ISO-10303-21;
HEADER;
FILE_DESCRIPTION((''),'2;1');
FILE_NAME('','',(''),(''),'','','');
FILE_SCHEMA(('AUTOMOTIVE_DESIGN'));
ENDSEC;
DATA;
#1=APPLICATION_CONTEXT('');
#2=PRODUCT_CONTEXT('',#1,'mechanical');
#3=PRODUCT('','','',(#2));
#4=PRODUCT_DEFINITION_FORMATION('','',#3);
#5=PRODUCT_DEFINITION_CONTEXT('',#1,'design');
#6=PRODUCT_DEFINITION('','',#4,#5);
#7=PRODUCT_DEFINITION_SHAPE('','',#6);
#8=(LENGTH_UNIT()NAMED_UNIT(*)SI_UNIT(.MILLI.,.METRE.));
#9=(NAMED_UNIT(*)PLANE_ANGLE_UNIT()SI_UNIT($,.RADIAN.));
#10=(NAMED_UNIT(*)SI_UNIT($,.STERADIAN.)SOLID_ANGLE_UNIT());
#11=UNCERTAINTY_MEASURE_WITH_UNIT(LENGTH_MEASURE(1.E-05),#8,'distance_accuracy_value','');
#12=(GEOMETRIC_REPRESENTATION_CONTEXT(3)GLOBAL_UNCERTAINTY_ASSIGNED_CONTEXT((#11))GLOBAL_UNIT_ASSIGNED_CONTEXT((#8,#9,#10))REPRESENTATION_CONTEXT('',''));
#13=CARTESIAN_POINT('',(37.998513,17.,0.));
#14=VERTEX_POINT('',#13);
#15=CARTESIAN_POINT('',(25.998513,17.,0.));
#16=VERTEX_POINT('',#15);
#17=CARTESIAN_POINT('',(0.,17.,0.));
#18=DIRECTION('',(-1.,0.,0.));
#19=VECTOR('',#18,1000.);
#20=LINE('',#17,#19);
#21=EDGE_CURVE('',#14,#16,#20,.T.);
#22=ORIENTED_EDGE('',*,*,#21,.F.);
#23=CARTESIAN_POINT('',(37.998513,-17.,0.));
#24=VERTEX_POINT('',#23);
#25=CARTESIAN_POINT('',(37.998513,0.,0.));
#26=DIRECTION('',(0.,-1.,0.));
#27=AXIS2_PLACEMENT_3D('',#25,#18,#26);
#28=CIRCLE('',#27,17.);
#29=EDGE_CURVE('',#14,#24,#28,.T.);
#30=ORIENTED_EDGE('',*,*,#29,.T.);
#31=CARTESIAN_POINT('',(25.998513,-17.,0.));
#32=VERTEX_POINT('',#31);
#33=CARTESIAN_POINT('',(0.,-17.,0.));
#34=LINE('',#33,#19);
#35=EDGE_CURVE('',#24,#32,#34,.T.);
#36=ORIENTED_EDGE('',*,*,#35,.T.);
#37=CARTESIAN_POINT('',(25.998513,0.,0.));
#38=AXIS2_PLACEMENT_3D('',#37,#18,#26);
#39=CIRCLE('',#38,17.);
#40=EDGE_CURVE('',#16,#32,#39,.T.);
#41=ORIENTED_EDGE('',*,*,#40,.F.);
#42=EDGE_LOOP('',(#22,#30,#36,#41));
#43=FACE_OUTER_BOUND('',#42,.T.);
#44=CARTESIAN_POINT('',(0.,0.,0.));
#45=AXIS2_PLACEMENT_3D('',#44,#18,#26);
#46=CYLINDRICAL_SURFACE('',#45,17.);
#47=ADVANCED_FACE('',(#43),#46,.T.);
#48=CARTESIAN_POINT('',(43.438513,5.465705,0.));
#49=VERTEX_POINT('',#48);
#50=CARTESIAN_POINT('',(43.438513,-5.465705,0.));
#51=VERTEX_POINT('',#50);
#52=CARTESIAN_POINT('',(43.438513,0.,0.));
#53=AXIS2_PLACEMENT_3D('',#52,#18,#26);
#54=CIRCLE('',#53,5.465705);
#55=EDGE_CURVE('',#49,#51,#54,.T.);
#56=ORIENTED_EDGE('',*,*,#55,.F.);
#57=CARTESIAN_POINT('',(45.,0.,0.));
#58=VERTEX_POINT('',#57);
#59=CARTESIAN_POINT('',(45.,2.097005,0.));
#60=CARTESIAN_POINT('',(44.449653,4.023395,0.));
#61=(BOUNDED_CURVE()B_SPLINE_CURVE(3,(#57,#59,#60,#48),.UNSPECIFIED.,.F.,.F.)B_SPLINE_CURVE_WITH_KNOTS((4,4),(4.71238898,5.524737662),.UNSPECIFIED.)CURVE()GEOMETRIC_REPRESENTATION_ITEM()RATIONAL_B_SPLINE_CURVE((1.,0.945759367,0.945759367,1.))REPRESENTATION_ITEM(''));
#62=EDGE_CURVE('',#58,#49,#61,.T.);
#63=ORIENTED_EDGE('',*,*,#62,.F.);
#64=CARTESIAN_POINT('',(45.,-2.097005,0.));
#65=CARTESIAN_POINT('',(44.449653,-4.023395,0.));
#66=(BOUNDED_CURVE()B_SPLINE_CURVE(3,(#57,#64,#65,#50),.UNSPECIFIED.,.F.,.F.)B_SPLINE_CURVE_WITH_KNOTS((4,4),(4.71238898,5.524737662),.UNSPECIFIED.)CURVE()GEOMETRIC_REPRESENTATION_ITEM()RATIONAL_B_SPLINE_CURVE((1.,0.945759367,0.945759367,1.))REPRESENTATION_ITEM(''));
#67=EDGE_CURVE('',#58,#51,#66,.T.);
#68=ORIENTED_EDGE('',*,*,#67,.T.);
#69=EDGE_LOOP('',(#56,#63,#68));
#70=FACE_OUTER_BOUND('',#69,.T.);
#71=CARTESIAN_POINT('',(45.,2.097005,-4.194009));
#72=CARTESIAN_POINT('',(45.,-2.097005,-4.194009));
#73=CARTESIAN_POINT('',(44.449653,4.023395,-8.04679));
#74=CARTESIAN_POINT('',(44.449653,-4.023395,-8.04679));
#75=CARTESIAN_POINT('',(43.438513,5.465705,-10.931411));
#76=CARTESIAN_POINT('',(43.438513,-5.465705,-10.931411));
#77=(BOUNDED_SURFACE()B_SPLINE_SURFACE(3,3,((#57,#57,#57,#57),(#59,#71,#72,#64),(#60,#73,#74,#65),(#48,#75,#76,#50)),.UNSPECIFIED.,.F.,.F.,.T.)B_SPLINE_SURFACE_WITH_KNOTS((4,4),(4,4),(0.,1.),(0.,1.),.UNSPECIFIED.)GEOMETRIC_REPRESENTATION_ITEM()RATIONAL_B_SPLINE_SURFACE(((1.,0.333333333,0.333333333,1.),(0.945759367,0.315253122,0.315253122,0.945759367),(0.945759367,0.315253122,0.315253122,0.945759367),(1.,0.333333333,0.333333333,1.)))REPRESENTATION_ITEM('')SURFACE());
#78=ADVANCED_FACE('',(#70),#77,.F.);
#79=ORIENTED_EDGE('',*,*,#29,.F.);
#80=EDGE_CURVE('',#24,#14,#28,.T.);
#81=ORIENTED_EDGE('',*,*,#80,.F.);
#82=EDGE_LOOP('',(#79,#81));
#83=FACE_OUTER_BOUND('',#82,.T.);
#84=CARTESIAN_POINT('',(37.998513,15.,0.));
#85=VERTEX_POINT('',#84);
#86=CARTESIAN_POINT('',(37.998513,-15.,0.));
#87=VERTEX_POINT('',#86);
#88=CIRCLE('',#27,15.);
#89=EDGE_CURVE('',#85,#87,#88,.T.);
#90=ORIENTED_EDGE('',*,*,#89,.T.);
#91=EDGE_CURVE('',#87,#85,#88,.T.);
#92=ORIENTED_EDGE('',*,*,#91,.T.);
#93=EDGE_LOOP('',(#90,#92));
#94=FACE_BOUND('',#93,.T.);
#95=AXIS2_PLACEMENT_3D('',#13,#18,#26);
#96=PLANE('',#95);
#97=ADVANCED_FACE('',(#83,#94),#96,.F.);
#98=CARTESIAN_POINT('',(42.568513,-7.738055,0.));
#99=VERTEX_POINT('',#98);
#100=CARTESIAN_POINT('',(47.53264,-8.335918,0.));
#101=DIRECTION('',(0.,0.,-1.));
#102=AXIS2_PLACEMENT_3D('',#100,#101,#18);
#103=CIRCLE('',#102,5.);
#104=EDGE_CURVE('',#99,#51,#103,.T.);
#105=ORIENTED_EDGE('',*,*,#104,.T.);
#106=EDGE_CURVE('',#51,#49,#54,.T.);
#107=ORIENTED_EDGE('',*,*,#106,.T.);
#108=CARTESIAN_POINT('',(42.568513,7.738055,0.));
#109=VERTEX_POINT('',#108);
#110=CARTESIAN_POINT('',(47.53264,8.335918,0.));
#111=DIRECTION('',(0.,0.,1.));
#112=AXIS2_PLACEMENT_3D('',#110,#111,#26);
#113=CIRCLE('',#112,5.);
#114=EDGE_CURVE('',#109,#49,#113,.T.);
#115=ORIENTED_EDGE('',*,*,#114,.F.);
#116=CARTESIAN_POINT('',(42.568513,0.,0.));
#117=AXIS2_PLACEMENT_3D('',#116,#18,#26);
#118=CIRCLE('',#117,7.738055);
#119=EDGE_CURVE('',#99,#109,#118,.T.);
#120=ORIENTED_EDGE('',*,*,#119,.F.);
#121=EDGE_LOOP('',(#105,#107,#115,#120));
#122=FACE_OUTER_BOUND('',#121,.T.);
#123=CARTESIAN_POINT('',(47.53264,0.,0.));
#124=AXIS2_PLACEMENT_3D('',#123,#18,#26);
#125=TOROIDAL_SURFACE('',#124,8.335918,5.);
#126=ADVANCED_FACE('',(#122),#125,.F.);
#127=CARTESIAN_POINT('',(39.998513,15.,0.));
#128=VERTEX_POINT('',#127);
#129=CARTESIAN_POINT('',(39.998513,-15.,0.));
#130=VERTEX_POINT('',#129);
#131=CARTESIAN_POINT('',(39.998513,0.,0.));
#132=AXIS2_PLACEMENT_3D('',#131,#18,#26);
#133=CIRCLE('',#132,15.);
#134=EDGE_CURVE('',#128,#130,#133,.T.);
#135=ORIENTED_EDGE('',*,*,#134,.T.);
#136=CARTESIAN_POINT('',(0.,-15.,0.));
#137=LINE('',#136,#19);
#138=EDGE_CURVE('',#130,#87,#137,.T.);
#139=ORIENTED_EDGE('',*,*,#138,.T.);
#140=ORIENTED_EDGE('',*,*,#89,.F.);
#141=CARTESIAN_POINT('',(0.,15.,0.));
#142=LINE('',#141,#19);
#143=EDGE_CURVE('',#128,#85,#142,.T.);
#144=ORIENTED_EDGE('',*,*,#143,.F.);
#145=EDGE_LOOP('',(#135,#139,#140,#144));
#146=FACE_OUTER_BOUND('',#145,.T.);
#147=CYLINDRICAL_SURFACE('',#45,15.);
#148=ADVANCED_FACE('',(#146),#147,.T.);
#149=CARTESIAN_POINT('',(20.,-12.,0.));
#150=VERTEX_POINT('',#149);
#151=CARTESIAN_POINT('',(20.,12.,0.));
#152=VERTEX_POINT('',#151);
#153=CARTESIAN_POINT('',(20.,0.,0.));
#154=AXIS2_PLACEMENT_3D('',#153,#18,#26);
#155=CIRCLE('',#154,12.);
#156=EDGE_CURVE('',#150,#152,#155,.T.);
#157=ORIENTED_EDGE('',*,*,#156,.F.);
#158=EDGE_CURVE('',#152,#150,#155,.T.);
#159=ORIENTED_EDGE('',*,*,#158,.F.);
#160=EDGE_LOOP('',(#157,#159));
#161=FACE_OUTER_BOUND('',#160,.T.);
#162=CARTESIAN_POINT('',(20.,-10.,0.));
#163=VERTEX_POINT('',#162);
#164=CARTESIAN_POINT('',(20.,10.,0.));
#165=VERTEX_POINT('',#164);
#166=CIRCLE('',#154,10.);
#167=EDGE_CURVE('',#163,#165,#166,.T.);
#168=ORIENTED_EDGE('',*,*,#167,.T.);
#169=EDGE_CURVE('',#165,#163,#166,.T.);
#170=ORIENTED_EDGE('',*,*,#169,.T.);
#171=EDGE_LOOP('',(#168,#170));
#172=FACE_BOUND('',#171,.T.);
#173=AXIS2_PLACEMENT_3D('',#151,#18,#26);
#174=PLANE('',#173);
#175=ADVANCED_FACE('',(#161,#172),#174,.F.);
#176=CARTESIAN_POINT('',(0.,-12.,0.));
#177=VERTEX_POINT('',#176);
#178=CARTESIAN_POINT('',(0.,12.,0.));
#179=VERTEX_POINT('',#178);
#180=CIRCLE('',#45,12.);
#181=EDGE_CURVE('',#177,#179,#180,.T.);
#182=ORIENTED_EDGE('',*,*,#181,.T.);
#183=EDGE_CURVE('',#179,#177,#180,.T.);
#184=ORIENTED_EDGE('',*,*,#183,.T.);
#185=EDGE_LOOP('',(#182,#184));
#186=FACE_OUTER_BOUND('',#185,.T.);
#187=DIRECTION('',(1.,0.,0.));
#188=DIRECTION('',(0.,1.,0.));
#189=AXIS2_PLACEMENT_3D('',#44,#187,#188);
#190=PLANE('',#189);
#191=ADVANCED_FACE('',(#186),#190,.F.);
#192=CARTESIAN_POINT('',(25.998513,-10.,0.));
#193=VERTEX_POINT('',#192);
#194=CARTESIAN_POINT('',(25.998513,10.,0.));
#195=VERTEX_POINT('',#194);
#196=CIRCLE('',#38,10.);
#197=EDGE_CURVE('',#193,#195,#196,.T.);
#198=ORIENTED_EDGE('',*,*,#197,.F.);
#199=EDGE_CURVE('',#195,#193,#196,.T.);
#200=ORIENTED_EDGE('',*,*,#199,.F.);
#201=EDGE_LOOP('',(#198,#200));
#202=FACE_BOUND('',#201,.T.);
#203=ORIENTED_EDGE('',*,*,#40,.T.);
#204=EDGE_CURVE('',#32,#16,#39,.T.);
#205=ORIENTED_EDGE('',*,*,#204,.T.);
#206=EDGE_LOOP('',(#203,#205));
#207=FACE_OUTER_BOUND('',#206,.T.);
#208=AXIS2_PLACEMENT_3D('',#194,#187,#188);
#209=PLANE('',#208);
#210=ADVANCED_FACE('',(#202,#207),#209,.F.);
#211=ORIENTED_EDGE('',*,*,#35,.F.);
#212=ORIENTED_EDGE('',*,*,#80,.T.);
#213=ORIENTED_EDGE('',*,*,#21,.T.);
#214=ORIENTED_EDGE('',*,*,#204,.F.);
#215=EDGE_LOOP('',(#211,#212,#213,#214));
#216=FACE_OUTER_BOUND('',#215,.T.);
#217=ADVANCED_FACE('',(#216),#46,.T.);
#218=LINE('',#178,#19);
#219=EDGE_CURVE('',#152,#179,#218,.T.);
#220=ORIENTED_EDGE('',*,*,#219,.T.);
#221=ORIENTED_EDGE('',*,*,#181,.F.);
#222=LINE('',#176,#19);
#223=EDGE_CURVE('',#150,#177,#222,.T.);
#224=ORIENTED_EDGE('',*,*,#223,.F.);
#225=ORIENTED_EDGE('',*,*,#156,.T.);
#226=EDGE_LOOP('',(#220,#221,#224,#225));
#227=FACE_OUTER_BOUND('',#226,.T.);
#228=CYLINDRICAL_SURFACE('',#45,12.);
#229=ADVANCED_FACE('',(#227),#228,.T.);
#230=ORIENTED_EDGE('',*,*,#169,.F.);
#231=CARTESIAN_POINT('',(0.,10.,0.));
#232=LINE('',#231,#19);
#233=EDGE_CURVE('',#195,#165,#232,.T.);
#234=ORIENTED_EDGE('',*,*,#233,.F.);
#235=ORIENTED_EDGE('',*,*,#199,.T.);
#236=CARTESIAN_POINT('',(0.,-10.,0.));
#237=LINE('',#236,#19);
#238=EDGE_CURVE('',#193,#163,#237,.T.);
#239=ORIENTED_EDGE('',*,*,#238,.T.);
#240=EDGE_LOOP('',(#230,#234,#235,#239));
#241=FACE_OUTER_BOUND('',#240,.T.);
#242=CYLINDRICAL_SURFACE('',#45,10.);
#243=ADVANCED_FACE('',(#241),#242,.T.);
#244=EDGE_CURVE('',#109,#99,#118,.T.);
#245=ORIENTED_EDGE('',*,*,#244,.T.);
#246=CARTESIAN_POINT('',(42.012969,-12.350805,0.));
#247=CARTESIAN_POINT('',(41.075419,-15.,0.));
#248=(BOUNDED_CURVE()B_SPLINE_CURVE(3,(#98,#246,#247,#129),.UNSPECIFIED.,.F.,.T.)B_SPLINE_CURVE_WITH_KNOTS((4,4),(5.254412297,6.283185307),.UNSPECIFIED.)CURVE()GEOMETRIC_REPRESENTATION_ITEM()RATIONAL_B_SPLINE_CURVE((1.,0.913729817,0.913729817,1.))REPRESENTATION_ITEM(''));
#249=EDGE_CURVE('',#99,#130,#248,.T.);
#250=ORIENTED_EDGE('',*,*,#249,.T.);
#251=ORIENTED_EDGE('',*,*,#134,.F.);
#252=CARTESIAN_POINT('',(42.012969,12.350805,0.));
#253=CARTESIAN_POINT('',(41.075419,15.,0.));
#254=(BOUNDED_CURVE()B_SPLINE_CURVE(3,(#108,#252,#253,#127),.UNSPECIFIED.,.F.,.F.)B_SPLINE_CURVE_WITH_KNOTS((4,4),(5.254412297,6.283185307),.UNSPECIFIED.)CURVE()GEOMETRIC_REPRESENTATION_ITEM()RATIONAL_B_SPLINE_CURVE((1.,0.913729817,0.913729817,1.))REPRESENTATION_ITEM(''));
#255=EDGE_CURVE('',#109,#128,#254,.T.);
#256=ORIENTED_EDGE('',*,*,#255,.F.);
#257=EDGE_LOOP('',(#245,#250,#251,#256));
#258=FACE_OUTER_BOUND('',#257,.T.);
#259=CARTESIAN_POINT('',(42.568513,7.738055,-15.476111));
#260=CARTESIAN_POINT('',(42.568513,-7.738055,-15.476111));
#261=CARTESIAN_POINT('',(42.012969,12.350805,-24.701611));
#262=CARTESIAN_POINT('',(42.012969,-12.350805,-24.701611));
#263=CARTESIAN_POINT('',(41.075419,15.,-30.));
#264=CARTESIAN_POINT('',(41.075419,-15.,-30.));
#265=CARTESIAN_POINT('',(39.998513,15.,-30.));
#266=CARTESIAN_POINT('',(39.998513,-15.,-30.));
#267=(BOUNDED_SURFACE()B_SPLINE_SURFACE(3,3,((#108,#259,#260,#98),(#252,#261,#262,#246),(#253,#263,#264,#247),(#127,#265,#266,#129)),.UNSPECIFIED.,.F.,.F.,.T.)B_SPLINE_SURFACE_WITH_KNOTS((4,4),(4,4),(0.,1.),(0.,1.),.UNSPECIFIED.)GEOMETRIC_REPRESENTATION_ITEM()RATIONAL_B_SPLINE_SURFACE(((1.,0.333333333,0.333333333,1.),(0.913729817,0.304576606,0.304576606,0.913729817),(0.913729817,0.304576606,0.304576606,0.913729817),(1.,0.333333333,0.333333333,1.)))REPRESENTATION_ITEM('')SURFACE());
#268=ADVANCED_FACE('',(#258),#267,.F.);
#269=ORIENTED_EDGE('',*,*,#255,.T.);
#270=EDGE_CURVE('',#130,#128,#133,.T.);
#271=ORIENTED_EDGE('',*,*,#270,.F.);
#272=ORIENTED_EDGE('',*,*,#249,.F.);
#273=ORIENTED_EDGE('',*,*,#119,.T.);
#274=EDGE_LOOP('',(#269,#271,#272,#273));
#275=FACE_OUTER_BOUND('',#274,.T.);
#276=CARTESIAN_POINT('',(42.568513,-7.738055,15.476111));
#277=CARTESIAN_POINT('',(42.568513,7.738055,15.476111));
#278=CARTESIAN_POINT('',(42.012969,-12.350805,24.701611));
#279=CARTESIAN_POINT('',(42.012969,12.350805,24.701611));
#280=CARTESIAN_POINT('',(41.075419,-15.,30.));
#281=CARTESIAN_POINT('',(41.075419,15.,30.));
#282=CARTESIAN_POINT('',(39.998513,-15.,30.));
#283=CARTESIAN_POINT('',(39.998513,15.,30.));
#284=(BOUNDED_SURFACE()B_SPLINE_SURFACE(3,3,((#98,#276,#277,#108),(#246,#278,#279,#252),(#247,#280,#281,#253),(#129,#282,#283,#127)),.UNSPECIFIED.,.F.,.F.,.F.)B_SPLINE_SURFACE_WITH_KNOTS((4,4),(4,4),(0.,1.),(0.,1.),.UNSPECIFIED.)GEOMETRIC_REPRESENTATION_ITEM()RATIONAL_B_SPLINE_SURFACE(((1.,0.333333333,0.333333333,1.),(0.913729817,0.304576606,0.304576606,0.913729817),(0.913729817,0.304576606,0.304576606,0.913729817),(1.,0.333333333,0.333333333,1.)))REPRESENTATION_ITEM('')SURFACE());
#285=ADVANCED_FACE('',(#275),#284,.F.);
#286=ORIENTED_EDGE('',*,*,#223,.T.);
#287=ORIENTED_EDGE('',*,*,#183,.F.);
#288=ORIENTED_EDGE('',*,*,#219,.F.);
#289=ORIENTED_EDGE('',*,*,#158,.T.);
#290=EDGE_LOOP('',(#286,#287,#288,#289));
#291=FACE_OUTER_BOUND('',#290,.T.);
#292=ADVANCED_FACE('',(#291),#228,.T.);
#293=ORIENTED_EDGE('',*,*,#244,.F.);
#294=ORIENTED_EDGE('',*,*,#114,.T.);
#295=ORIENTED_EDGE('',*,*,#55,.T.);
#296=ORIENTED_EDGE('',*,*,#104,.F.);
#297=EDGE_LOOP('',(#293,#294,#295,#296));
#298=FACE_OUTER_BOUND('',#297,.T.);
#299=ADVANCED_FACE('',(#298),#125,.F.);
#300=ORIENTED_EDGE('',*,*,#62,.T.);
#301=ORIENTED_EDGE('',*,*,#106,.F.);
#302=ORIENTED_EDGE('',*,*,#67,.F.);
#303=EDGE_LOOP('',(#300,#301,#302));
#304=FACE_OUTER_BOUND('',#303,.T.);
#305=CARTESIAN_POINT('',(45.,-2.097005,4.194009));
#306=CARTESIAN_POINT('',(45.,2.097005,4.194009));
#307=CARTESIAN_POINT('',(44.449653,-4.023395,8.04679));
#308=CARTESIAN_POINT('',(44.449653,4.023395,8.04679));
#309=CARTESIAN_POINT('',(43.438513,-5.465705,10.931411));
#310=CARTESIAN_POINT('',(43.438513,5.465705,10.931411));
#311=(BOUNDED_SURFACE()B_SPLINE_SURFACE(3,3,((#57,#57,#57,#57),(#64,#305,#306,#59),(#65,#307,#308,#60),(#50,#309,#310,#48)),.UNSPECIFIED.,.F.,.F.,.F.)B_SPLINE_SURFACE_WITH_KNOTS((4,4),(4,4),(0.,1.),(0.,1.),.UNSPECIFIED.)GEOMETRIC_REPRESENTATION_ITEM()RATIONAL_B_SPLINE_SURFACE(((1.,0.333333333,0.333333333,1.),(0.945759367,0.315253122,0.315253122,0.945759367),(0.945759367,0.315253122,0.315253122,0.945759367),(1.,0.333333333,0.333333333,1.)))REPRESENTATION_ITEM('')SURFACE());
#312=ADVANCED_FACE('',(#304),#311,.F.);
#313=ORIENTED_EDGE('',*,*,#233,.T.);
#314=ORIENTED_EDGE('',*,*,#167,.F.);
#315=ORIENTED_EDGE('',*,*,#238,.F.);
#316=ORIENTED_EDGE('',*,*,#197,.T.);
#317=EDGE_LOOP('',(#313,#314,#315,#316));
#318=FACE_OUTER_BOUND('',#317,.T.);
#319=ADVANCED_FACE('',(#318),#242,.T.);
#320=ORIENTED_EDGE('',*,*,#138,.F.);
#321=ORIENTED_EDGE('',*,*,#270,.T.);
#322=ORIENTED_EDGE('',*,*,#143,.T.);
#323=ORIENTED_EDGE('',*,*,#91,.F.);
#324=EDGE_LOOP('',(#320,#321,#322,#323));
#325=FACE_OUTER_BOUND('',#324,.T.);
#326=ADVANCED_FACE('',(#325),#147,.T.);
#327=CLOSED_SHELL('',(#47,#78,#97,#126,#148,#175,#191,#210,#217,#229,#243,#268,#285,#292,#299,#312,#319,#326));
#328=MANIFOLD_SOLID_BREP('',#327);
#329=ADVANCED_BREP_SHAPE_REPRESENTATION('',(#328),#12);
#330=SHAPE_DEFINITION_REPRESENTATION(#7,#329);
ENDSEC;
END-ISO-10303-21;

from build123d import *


with BuildPart() as part:
    # Sketch1 → Revolve1 (revolve)
    with BuildSketch(Plane.XY, mode=Mode.PRIVATE) as revolve1_sk:
        with BuildLine():
            Line((0, 0), (0, 12))
            Line((0, 12), (20, 12))
            Line((20, 12), (20, 10))
            Line((20, 10), (25.99851273, 10))
            Line((25.99851273, 10), (25.99851273, 17))
            Line((25.99851273, 17), (37.99851273, 17))
            Line((37.99851273, 17), (37.99851273, 15))
            Line((37.99851273, 15), (39.99851273, 15))
            add(Edge.make_bspline(
                [(42.56851273, 7.738055311), (41.693908377, 15), (39.99851273, 15)],
                knots=[2.112819643, 2.112819643, 2.112819643, 3.141592654, 3.141592654, 3.141592654], degree=2, weights=[1, 0.870594726, 1]))
            ThreePointArc((42.56851273, 7.738055311), (42.863176718, 6.548150813), (43.43851273, 5.465705407))
            add(Edge.make_bspline(
                [(45, 0), (45, 3.238369631), (43.43851273, 5.465705407)],
                knots=[4.71238898, 4.71238898, 4.71238898, 5.524737662, 5.524737662, 5.524737662], degree=2, weights=[1, 0.918639051, 1]))
            Line((45, 0), (0, 0))
        make_face()
    revolve(revolve1_sk.sketch.rotate(Axis((0, 0, 0), (1, 0, 0)), 180), axis=Axis((0, 0, 0), (1, 0, 0)))


solid = part.part
